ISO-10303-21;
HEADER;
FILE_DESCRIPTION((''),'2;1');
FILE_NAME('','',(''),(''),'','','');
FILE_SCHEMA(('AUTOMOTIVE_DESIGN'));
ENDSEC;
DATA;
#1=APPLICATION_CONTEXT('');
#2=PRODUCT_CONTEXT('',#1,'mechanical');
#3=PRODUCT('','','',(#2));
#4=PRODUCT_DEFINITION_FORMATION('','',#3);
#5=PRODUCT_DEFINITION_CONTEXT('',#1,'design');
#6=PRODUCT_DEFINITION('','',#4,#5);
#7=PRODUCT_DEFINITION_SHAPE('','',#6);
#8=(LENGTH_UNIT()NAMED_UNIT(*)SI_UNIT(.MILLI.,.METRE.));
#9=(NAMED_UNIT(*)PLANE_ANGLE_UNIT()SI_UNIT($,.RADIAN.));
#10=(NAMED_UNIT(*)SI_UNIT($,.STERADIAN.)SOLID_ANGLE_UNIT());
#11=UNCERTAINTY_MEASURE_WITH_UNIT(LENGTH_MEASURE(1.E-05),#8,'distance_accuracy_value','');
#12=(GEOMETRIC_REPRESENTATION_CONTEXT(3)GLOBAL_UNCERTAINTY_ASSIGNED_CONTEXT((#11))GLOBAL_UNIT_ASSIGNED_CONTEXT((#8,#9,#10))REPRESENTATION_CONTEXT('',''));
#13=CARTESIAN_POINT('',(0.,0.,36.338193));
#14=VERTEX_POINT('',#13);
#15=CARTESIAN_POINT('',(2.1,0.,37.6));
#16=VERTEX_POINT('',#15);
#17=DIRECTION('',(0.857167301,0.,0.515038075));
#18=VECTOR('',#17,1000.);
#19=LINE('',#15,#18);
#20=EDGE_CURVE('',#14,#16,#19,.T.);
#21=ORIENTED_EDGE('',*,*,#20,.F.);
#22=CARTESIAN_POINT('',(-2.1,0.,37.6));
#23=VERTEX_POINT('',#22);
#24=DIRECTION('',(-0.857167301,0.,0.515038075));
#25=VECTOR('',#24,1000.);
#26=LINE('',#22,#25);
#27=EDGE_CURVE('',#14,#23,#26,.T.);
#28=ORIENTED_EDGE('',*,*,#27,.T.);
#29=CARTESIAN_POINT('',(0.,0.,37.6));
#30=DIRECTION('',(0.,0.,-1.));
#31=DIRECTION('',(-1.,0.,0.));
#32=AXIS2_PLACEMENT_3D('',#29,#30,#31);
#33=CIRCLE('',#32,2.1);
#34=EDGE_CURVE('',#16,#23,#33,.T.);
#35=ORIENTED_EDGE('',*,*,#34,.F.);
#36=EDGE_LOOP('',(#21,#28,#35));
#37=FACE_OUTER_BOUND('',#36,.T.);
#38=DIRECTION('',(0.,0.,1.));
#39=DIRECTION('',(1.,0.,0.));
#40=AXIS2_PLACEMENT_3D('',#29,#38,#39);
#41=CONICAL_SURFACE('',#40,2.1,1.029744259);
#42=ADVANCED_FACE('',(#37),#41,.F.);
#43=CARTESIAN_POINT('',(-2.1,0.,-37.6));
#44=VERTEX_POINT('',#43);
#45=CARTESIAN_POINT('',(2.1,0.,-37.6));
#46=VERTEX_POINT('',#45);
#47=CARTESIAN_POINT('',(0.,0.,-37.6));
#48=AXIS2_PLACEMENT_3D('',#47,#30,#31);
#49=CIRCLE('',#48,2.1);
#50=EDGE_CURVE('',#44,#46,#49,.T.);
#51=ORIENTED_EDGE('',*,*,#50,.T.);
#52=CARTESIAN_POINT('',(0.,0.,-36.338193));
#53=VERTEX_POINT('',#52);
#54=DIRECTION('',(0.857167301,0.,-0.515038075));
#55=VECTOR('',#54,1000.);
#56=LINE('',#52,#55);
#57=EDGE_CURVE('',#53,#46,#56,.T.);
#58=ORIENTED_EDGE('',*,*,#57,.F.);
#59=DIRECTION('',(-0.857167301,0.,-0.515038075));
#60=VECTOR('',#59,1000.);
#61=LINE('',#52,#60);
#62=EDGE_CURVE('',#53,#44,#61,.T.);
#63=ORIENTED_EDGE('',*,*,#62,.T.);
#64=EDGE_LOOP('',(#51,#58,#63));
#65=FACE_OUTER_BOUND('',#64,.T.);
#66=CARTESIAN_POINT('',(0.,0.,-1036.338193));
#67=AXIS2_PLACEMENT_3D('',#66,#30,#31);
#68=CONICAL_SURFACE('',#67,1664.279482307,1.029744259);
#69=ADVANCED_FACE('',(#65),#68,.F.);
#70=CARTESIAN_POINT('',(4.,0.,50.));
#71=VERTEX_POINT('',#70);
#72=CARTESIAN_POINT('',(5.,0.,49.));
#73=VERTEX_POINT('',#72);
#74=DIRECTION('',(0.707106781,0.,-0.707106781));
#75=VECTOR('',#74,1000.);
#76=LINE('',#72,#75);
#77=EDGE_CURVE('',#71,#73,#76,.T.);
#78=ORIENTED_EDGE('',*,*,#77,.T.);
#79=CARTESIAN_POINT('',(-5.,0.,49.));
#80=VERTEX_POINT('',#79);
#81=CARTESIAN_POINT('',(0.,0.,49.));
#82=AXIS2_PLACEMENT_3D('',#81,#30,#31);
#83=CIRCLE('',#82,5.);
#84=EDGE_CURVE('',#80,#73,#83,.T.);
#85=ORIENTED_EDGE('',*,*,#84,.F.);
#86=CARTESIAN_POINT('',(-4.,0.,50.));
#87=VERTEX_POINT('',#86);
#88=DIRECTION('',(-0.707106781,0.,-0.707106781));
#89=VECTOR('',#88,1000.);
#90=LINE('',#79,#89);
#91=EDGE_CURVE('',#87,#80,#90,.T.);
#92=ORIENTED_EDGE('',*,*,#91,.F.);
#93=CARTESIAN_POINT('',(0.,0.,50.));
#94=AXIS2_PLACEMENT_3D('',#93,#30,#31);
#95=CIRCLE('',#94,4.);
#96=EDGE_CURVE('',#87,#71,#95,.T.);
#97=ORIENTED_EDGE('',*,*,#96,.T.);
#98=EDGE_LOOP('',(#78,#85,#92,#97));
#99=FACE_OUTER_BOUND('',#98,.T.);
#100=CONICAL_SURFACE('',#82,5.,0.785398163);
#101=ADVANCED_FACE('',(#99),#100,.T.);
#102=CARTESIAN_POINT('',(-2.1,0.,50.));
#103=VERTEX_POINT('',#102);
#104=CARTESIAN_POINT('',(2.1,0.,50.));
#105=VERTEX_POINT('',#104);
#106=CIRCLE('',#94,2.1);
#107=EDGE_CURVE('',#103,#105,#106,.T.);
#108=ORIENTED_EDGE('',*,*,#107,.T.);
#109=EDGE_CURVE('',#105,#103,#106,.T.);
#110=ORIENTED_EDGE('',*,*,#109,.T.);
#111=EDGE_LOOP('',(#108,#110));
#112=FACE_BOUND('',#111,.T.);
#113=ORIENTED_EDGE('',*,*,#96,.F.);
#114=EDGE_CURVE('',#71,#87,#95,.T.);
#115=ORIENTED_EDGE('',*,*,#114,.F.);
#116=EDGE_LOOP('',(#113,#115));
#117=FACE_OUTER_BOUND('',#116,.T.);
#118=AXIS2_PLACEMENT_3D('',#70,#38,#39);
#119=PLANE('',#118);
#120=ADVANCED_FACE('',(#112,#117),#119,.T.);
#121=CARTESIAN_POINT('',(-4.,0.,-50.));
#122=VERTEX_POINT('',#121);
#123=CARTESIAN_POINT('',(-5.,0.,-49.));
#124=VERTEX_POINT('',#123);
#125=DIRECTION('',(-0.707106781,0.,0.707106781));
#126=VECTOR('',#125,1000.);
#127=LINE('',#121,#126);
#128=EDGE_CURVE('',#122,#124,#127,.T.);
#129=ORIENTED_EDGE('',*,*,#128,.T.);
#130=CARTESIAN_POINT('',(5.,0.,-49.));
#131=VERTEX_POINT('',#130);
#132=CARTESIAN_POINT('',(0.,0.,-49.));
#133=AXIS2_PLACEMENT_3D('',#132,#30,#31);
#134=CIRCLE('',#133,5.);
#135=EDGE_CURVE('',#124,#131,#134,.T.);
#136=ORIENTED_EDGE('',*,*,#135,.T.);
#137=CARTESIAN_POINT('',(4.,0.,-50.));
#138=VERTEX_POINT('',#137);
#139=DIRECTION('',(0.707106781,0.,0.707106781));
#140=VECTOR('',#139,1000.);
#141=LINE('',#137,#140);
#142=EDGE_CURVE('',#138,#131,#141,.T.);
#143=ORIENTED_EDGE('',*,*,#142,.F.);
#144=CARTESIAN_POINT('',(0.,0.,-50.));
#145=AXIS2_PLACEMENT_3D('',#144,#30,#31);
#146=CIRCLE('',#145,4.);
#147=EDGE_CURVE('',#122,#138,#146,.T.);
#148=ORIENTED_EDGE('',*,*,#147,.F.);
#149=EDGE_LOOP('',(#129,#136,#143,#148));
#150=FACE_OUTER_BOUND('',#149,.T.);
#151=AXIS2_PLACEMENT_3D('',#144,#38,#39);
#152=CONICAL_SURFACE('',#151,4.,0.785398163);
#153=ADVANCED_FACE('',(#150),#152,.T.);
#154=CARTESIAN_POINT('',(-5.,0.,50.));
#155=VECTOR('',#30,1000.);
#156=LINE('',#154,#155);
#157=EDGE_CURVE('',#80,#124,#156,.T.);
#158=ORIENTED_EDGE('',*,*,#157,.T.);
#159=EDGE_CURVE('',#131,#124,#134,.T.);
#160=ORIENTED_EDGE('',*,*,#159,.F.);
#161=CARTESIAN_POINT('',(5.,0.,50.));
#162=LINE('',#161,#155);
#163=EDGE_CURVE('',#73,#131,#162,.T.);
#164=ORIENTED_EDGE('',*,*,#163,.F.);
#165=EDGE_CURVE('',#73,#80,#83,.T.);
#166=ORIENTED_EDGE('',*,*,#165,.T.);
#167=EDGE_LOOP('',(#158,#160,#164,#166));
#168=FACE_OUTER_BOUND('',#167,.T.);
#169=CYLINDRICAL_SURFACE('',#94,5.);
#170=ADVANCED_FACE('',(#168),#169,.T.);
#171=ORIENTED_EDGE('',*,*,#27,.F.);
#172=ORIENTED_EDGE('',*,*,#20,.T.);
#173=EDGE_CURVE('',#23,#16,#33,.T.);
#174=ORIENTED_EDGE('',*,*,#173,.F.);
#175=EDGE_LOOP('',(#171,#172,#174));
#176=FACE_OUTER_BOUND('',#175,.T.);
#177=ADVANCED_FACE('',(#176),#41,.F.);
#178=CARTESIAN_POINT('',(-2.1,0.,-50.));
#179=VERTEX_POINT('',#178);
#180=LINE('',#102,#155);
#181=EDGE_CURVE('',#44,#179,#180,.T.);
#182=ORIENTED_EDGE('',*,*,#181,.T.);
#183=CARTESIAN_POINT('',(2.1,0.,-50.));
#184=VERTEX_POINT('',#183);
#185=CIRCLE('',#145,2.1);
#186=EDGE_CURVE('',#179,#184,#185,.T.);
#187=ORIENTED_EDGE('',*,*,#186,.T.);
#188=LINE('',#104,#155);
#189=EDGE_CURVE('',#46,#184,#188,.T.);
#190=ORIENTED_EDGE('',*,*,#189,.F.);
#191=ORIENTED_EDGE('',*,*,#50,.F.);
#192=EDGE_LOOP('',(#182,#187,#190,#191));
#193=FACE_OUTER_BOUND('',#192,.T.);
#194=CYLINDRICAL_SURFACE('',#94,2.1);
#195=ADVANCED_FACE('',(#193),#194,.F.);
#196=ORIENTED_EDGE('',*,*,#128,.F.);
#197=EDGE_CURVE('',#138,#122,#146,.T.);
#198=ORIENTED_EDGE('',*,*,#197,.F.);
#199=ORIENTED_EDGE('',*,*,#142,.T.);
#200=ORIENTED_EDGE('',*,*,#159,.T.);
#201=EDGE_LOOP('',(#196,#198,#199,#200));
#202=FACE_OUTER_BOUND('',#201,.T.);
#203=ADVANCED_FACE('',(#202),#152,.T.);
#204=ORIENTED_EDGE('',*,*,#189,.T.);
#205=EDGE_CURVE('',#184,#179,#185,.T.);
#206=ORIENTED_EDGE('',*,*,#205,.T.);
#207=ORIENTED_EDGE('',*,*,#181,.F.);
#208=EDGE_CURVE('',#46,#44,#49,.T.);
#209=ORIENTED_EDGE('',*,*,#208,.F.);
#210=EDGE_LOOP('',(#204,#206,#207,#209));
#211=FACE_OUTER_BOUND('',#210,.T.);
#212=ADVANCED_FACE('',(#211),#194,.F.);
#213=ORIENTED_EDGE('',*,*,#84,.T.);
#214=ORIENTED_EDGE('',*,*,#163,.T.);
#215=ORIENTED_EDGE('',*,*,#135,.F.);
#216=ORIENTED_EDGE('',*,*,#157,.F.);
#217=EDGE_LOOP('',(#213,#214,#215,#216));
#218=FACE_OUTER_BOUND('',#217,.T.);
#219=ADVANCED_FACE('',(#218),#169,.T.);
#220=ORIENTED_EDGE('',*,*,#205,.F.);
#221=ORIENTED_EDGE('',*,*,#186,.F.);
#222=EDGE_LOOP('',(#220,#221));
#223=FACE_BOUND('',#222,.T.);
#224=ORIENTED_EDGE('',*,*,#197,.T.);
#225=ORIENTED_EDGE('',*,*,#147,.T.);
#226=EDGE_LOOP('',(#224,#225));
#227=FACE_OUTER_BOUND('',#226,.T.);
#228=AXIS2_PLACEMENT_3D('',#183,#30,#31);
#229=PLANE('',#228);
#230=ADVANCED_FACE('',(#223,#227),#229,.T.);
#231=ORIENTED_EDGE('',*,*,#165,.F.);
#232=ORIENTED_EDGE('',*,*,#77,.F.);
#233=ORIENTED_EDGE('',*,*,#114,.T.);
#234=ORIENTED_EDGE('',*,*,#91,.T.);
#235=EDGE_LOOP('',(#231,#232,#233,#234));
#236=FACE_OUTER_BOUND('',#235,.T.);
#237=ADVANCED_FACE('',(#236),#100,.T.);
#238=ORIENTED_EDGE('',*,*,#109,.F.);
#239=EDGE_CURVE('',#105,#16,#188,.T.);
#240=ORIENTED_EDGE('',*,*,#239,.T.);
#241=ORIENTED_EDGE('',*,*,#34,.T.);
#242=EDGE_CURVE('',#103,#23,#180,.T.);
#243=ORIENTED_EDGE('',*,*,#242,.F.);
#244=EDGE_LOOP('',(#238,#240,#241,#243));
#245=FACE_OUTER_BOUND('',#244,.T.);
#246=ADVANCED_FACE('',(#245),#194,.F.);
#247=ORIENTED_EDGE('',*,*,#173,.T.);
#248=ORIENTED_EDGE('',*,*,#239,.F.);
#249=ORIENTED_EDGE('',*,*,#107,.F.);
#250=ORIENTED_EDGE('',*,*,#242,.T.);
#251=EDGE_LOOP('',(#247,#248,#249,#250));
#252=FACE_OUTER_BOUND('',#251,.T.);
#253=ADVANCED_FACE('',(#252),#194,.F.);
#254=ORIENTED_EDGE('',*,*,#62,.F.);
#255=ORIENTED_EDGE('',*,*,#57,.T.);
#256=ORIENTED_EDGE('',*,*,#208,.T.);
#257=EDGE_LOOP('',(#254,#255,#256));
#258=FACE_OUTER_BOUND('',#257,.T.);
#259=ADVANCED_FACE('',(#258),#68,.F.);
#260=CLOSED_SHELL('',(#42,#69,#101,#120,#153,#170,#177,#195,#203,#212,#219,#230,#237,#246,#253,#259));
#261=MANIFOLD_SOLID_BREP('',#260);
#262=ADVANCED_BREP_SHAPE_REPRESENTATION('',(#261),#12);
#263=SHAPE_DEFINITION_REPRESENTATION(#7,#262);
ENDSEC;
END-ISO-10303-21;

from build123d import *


with BuildPart() as part:
    # 草图1 → 旋转1 (revolve)
    with BuildSketch(Plane.XZ, mode=Mode.PRIVATE) as revolve_1_sk:
        Polygon((2.1, 37.6), (0, 36.3381927), (0, -36.3381927), (2.1, -37.6), (2.1, -50), (4, -50), (5, -49), (5, 49), (4, 50), (2.1, 50), align=None)
    revolve(revolve_1_sk.sketch.rotate(Axis((0, 0, 50), (0, 0, -1)), 180), axis=Axis((0, 0, 50), (0, 0, -1)))


solid = part.part
